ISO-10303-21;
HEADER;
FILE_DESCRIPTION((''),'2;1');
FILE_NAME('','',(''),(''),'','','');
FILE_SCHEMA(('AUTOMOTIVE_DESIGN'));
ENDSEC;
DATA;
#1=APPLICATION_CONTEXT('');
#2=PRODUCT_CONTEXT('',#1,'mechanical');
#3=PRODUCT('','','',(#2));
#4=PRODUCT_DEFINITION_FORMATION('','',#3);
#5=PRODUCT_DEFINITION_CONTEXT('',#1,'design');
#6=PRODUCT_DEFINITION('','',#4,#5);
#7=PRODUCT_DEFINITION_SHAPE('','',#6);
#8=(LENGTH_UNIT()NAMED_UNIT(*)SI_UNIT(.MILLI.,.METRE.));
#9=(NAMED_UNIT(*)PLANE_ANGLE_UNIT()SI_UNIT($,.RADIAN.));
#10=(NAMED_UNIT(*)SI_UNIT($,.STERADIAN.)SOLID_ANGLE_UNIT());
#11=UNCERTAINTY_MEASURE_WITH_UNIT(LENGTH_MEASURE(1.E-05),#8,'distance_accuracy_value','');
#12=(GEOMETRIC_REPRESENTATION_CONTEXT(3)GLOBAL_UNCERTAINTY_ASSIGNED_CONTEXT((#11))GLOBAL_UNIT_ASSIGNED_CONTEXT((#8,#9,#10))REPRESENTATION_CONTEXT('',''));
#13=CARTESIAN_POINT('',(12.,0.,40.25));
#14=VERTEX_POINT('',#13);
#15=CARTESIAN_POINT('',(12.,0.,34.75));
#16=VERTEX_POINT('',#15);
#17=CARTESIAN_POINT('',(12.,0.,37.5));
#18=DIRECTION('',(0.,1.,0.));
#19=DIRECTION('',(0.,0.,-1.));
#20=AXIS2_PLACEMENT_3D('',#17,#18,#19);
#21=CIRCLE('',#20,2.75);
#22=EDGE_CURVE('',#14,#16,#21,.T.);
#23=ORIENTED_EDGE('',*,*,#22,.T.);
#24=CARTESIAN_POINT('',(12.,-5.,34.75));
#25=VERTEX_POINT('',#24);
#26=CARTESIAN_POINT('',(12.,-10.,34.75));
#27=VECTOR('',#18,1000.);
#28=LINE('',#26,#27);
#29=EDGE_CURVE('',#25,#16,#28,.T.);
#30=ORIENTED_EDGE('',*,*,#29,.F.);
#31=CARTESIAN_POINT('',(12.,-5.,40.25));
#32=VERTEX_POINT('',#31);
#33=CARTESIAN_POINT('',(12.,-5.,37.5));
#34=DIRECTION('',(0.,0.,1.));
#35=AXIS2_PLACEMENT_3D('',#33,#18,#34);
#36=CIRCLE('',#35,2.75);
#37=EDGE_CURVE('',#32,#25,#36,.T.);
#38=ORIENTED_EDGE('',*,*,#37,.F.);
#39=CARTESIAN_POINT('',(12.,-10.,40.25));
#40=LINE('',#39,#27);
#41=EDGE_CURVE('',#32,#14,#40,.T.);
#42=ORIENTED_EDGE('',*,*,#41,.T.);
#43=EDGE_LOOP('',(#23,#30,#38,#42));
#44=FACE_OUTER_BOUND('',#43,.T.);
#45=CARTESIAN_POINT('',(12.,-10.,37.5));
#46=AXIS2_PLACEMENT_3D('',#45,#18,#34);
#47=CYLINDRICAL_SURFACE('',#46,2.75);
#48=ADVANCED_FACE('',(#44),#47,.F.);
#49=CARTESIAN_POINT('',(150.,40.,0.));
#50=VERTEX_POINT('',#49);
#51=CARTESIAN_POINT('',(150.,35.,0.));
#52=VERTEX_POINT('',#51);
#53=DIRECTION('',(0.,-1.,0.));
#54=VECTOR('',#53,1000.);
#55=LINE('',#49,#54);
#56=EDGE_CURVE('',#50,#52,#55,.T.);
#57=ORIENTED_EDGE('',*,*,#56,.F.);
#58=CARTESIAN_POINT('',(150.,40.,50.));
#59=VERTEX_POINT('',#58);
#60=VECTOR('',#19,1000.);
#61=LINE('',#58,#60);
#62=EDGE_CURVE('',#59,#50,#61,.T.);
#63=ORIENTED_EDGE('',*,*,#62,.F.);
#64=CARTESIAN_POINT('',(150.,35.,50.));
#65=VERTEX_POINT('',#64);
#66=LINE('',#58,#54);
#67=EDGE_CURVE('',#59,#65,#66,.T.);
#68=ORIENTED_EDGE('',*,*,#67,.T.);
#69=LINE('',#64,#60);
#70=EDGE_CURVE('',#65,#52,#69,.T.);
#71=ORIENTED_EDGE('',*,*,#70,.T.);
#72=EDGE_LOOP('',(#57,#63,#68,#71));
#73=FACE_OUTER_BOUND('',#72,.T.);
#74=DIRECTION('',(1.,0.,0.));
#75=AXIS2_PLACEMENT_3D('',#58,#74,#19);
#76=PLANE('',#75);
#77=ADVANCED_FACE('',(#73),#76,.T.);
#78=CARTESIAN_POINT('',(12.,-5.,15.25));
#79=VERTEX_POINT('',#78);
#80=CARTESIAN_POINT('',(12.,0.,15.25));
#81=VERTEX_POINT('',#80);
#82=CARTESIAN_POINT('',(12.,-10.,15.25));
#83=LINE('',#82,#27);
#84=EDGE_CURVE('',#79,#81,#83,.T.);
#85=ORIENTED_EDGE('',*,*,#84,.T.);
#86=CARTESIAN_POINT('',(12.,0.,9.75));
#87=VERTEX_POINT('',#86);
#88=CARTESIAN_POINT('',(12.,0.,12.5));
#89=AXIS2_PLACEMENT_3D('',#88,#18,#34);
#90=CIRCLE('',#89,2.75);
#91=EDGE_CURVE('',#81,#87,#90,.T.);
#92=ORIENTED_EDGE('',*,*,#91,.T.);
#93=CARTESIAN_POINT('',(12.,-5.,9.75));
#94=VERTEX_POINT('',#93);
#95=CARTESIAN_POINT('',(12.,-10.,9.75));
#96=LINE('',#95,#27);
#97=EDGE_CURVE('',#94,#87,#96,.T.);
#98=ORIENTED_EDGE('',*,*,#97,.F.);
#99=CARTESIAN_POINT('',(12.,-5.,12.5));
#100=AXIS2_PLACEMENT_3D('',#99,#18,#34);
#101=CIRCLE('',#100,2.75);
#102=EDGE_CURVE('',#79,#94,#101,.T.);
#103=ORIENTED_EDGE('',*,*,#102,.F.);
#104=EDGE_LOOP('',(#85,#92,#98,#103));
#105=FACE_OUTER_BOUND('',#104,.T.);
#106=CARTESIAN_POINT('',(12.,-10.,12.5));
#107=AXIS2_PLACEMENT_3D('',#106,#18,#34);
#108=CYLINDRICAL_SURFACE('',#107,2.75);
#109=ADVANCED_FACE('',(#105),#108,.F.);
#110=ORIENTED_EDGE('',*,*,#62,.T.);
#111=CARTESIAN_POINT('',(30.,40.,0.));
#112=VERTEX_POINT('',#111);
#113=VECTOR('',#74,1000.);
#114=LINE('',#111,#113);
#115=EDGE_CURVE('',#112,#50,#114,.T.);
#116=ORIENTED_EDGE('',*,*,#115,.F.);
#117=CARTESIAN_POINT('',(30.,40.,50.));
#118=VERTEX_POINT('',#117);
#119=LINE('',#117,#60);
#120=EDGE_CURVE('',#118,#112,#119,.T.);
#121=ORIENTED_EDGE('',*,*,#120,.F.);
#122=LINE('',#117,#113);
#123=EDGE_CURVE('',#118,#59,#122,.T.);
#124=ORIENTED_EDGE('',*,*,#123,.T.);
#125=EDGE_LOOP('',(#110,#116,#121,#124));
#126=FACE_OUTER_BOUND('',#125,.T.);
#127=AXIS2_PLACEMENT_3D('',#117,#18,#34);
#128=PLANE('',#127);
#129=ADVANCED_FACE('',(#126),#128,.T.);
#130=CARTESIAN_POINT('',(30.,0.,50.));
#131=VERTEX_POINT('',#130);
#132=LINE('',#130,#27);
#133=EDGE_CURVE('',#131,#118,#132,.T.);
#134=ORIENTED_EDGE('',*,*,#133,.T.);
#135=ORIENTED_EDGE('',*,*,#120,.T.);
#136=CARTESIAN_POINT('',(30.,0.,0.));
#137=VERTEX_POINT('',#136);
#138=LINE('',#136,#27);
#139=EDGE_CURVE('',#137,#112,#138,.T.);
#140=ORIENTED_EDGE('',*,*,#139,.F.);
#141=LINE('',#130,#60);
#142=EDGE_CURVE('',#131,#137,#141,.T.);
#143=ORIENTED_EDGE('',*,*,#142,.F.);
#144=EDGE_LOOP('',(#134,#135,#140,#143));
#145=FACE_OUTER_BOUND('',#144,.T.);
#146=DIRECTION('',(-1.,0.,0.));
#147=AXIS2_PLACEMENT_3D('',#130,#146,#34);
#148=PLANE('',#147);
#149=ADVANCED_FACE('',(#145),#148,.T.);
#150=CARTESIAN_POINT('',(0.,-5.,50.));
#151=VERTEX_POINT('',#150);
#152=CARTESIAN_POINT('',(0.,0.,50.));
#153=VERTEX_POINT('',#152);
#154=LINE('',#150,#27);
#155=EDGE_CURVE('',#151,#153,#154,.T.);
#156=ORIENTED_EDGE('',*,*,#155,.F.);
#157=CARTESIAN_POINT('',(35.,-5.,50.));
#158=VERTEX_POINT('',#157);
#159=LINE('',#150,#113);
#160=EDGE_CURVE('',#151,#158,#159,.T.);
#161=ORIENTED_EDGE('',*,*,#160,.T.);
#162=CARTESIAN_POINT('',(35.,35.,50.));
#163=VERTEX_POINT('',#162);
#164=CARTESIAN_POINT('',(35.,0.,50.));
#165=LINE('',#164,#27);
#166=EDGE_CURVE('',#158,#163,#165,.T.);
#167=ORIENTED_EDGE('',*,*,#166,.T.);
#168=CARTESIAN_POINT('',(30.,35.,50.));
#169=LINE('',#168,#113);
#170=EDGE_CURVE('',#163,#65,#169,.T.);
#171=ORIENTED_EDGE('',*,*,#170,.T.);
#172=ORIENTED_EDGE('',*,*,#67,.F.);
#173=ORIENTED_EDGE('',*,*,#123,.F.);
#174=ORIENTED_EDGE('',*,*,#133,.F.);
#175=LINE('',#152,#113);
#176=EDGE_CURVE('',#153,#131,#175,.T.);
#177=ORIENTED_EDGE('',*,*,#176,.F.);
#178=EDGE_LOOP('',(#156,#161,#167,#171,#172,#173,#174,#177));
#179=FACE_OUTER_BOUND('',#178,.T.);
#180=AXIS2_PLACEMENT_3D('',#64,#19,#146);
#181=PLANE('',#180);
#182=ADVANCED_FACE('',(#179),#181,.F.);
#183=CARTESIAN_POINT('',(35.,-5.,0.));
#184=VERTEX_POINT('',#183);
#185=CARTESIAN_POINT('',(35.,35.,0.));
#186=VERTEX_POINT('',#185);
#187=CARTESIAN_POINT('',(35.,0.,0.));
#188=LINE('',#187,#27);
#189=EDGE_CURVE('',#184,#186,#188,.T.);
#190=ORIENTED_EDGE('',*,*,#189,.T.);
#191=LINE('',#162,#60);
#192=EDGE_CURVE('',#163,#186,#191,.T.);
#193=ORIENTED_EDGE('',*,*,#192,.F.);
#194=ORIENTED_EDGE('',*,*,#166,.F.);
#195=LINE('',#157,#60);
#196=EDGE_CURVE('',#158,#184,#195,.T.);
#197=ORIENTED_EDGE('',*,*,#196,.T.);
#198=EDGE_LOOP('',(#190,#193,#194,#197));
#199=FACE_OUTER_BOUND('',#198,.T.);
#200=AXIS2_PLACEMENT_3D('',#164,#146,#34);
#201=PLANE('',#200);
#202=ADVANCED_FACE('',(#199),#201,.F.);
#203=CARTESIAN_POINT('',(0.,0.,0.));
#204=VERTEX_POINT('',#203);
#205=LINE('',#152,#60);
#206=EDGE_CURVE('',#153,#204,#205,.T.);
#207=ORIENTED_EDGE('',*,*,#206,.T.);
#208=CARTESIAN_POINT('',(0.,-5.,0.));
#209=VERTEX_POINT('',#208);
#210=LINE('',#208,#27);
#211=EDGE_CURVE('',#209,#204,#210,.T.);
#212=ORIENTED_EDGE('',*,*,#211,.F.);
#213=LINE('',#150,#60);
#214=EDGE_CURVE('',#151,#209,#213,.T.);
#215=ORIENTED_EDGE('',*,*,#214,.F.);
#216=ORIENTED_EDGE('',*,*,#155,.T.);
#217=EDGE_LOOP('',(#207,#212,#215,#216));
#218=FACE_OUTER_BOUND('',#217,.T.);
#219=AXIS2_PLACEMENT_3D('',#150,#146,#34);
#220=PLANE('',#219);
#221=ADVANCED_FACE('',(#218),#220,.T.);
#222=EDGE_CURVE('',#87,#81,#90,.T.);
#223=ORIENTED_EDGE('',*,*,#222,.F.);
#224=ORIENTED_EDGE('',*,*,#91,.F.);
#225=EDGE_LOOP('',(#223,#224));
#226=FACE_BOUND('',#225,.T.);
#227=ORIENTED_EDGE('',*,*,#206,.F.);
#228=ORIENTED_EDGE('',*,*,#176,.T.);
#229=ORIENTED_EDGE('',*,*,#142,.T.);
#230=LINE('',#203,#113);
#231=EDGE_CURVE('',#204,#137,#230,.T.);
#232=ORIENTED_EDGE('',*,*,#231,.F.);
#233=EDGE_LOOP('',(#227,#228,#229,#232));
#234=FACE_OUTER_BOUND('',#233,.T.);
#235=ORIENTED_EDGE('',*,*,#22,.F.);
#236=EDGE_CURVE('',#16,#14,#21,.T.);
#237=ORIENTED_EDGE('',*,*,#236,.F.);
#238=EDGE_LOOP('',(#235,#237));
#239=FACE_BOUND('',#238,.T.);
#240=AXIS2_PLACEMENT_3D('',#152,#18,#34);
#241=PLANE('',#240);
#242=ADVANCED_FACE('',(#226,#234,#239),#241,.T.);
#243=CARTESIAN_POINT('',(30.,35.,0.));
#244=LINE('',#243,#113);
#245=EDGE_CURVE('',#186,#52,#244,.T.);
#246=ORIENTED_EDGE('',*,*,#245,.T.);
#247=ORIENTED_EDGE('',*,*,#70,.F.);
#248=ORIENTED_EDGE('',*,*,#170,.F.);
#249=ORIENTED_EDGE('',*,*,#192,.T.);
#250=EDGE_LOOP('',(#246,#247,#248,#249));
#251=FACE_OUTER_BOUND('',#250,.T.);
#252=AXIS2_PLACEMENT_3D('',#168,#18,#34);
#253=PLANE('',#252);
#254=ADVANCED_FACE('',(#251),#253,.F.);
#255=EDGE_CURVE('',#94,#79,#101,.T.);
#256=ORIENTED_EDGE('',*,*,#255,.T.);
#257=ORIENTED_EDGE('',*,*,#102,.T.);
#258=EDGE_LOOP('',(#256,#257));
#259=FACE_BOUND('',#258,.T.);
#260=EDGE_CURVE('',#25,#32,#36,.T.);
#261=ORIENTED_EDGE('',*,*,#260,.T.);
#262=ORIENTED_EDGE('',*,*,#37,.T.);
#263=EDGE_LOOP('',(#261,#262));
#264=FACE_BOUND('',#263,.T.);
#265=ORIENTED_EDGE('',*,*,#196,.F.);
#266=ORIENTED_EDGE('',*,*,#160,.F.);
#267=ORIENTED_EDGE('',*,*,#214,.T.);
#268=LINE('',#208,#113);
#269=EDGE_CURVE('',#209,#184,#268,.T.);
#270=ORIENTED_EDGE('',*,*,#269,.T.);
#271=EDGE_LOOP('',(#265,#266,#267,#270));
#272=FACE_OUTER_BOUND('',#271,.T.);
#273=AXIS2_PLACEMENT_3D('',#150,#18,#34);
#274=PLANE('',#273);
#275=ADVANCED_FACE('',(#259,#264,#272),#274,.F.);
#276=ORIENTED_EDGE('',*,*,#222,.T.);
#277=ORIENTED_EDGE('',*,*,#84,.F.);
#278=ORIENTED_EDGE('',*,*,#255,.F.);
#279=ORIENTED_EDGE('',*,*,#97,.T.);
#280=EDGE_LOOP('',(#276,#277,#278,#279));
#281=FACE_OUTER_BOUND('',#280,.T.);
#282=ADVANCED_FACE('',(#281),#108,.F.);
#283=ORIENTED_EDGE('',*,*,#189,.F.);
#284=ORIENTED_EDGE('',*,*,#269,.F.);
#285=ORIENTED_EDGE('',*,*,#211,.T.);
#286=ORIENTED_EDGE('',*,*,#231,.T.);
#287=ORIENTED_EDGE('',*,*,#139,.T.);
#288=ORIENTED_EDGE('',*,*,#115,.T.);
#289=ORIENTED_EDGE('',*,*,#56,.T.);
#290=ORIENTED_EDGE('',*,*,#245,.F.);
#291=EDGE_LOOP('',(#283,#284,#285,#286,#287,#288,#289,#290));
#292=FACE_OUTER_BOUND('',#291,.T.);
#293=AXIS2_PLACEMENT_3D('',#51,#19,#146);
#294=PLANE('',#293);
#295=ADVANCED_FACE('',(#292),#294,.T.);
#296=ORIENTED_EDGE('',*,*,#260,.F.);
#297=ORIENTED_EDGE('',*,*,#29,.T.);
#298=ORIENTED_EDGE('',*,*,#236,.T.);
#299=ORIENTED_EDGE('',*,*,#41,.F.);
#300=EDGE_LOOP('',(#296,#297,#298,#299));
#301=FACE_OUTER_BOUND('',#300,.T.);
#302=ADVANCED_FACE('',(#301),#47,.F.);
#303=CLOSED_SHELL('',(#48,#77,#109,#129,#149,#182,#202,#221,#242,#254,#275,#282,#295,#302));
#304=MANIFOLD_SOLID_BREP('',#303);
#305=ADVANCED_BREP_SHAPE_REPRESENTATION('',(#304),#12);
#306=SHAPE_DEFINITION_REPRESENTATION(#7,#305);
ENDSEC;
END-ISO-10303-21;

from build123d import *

# Parameters (mm, degrees)
EXTRUDE_1_DEPTH     = 50
SKETCH_2_R          = 2.75
CUT_EXTRUDE_1_DEPTH = 10


with BuildPart() as part:
    # 草图1 → 拉伸-薄壁1 (new body)
    with BuildSketch(Plane.XY):
        Polygon((0, 0), (30, 0), (30, 40), (150, 40), (150, 35), (35, 35), (35, -5), (0, -5), align=None)
    extrude(amount=EXTRUDE_1_DEPTH)

    # 草图2 → 切除-拉伸1 (cut)
    with BuildSketch(Plane(origin=(0, 0, 0), x_dir=(1, 0, 0), z_dir=(0, 1, 0))):
        with Locations(Location((12, -12.5, 0), (0, 0, 270))):
            Circle(SKETCH_2_R)
        with Locations(Location((12, -37.5, 0), (0, 0, 270))):
            Circle(SKETCH_2_R)
    extrude(amount=-CUT_EXTRUDE_1_DEPTH, mode=Mode.SUBTRACT)


solid = part.part
